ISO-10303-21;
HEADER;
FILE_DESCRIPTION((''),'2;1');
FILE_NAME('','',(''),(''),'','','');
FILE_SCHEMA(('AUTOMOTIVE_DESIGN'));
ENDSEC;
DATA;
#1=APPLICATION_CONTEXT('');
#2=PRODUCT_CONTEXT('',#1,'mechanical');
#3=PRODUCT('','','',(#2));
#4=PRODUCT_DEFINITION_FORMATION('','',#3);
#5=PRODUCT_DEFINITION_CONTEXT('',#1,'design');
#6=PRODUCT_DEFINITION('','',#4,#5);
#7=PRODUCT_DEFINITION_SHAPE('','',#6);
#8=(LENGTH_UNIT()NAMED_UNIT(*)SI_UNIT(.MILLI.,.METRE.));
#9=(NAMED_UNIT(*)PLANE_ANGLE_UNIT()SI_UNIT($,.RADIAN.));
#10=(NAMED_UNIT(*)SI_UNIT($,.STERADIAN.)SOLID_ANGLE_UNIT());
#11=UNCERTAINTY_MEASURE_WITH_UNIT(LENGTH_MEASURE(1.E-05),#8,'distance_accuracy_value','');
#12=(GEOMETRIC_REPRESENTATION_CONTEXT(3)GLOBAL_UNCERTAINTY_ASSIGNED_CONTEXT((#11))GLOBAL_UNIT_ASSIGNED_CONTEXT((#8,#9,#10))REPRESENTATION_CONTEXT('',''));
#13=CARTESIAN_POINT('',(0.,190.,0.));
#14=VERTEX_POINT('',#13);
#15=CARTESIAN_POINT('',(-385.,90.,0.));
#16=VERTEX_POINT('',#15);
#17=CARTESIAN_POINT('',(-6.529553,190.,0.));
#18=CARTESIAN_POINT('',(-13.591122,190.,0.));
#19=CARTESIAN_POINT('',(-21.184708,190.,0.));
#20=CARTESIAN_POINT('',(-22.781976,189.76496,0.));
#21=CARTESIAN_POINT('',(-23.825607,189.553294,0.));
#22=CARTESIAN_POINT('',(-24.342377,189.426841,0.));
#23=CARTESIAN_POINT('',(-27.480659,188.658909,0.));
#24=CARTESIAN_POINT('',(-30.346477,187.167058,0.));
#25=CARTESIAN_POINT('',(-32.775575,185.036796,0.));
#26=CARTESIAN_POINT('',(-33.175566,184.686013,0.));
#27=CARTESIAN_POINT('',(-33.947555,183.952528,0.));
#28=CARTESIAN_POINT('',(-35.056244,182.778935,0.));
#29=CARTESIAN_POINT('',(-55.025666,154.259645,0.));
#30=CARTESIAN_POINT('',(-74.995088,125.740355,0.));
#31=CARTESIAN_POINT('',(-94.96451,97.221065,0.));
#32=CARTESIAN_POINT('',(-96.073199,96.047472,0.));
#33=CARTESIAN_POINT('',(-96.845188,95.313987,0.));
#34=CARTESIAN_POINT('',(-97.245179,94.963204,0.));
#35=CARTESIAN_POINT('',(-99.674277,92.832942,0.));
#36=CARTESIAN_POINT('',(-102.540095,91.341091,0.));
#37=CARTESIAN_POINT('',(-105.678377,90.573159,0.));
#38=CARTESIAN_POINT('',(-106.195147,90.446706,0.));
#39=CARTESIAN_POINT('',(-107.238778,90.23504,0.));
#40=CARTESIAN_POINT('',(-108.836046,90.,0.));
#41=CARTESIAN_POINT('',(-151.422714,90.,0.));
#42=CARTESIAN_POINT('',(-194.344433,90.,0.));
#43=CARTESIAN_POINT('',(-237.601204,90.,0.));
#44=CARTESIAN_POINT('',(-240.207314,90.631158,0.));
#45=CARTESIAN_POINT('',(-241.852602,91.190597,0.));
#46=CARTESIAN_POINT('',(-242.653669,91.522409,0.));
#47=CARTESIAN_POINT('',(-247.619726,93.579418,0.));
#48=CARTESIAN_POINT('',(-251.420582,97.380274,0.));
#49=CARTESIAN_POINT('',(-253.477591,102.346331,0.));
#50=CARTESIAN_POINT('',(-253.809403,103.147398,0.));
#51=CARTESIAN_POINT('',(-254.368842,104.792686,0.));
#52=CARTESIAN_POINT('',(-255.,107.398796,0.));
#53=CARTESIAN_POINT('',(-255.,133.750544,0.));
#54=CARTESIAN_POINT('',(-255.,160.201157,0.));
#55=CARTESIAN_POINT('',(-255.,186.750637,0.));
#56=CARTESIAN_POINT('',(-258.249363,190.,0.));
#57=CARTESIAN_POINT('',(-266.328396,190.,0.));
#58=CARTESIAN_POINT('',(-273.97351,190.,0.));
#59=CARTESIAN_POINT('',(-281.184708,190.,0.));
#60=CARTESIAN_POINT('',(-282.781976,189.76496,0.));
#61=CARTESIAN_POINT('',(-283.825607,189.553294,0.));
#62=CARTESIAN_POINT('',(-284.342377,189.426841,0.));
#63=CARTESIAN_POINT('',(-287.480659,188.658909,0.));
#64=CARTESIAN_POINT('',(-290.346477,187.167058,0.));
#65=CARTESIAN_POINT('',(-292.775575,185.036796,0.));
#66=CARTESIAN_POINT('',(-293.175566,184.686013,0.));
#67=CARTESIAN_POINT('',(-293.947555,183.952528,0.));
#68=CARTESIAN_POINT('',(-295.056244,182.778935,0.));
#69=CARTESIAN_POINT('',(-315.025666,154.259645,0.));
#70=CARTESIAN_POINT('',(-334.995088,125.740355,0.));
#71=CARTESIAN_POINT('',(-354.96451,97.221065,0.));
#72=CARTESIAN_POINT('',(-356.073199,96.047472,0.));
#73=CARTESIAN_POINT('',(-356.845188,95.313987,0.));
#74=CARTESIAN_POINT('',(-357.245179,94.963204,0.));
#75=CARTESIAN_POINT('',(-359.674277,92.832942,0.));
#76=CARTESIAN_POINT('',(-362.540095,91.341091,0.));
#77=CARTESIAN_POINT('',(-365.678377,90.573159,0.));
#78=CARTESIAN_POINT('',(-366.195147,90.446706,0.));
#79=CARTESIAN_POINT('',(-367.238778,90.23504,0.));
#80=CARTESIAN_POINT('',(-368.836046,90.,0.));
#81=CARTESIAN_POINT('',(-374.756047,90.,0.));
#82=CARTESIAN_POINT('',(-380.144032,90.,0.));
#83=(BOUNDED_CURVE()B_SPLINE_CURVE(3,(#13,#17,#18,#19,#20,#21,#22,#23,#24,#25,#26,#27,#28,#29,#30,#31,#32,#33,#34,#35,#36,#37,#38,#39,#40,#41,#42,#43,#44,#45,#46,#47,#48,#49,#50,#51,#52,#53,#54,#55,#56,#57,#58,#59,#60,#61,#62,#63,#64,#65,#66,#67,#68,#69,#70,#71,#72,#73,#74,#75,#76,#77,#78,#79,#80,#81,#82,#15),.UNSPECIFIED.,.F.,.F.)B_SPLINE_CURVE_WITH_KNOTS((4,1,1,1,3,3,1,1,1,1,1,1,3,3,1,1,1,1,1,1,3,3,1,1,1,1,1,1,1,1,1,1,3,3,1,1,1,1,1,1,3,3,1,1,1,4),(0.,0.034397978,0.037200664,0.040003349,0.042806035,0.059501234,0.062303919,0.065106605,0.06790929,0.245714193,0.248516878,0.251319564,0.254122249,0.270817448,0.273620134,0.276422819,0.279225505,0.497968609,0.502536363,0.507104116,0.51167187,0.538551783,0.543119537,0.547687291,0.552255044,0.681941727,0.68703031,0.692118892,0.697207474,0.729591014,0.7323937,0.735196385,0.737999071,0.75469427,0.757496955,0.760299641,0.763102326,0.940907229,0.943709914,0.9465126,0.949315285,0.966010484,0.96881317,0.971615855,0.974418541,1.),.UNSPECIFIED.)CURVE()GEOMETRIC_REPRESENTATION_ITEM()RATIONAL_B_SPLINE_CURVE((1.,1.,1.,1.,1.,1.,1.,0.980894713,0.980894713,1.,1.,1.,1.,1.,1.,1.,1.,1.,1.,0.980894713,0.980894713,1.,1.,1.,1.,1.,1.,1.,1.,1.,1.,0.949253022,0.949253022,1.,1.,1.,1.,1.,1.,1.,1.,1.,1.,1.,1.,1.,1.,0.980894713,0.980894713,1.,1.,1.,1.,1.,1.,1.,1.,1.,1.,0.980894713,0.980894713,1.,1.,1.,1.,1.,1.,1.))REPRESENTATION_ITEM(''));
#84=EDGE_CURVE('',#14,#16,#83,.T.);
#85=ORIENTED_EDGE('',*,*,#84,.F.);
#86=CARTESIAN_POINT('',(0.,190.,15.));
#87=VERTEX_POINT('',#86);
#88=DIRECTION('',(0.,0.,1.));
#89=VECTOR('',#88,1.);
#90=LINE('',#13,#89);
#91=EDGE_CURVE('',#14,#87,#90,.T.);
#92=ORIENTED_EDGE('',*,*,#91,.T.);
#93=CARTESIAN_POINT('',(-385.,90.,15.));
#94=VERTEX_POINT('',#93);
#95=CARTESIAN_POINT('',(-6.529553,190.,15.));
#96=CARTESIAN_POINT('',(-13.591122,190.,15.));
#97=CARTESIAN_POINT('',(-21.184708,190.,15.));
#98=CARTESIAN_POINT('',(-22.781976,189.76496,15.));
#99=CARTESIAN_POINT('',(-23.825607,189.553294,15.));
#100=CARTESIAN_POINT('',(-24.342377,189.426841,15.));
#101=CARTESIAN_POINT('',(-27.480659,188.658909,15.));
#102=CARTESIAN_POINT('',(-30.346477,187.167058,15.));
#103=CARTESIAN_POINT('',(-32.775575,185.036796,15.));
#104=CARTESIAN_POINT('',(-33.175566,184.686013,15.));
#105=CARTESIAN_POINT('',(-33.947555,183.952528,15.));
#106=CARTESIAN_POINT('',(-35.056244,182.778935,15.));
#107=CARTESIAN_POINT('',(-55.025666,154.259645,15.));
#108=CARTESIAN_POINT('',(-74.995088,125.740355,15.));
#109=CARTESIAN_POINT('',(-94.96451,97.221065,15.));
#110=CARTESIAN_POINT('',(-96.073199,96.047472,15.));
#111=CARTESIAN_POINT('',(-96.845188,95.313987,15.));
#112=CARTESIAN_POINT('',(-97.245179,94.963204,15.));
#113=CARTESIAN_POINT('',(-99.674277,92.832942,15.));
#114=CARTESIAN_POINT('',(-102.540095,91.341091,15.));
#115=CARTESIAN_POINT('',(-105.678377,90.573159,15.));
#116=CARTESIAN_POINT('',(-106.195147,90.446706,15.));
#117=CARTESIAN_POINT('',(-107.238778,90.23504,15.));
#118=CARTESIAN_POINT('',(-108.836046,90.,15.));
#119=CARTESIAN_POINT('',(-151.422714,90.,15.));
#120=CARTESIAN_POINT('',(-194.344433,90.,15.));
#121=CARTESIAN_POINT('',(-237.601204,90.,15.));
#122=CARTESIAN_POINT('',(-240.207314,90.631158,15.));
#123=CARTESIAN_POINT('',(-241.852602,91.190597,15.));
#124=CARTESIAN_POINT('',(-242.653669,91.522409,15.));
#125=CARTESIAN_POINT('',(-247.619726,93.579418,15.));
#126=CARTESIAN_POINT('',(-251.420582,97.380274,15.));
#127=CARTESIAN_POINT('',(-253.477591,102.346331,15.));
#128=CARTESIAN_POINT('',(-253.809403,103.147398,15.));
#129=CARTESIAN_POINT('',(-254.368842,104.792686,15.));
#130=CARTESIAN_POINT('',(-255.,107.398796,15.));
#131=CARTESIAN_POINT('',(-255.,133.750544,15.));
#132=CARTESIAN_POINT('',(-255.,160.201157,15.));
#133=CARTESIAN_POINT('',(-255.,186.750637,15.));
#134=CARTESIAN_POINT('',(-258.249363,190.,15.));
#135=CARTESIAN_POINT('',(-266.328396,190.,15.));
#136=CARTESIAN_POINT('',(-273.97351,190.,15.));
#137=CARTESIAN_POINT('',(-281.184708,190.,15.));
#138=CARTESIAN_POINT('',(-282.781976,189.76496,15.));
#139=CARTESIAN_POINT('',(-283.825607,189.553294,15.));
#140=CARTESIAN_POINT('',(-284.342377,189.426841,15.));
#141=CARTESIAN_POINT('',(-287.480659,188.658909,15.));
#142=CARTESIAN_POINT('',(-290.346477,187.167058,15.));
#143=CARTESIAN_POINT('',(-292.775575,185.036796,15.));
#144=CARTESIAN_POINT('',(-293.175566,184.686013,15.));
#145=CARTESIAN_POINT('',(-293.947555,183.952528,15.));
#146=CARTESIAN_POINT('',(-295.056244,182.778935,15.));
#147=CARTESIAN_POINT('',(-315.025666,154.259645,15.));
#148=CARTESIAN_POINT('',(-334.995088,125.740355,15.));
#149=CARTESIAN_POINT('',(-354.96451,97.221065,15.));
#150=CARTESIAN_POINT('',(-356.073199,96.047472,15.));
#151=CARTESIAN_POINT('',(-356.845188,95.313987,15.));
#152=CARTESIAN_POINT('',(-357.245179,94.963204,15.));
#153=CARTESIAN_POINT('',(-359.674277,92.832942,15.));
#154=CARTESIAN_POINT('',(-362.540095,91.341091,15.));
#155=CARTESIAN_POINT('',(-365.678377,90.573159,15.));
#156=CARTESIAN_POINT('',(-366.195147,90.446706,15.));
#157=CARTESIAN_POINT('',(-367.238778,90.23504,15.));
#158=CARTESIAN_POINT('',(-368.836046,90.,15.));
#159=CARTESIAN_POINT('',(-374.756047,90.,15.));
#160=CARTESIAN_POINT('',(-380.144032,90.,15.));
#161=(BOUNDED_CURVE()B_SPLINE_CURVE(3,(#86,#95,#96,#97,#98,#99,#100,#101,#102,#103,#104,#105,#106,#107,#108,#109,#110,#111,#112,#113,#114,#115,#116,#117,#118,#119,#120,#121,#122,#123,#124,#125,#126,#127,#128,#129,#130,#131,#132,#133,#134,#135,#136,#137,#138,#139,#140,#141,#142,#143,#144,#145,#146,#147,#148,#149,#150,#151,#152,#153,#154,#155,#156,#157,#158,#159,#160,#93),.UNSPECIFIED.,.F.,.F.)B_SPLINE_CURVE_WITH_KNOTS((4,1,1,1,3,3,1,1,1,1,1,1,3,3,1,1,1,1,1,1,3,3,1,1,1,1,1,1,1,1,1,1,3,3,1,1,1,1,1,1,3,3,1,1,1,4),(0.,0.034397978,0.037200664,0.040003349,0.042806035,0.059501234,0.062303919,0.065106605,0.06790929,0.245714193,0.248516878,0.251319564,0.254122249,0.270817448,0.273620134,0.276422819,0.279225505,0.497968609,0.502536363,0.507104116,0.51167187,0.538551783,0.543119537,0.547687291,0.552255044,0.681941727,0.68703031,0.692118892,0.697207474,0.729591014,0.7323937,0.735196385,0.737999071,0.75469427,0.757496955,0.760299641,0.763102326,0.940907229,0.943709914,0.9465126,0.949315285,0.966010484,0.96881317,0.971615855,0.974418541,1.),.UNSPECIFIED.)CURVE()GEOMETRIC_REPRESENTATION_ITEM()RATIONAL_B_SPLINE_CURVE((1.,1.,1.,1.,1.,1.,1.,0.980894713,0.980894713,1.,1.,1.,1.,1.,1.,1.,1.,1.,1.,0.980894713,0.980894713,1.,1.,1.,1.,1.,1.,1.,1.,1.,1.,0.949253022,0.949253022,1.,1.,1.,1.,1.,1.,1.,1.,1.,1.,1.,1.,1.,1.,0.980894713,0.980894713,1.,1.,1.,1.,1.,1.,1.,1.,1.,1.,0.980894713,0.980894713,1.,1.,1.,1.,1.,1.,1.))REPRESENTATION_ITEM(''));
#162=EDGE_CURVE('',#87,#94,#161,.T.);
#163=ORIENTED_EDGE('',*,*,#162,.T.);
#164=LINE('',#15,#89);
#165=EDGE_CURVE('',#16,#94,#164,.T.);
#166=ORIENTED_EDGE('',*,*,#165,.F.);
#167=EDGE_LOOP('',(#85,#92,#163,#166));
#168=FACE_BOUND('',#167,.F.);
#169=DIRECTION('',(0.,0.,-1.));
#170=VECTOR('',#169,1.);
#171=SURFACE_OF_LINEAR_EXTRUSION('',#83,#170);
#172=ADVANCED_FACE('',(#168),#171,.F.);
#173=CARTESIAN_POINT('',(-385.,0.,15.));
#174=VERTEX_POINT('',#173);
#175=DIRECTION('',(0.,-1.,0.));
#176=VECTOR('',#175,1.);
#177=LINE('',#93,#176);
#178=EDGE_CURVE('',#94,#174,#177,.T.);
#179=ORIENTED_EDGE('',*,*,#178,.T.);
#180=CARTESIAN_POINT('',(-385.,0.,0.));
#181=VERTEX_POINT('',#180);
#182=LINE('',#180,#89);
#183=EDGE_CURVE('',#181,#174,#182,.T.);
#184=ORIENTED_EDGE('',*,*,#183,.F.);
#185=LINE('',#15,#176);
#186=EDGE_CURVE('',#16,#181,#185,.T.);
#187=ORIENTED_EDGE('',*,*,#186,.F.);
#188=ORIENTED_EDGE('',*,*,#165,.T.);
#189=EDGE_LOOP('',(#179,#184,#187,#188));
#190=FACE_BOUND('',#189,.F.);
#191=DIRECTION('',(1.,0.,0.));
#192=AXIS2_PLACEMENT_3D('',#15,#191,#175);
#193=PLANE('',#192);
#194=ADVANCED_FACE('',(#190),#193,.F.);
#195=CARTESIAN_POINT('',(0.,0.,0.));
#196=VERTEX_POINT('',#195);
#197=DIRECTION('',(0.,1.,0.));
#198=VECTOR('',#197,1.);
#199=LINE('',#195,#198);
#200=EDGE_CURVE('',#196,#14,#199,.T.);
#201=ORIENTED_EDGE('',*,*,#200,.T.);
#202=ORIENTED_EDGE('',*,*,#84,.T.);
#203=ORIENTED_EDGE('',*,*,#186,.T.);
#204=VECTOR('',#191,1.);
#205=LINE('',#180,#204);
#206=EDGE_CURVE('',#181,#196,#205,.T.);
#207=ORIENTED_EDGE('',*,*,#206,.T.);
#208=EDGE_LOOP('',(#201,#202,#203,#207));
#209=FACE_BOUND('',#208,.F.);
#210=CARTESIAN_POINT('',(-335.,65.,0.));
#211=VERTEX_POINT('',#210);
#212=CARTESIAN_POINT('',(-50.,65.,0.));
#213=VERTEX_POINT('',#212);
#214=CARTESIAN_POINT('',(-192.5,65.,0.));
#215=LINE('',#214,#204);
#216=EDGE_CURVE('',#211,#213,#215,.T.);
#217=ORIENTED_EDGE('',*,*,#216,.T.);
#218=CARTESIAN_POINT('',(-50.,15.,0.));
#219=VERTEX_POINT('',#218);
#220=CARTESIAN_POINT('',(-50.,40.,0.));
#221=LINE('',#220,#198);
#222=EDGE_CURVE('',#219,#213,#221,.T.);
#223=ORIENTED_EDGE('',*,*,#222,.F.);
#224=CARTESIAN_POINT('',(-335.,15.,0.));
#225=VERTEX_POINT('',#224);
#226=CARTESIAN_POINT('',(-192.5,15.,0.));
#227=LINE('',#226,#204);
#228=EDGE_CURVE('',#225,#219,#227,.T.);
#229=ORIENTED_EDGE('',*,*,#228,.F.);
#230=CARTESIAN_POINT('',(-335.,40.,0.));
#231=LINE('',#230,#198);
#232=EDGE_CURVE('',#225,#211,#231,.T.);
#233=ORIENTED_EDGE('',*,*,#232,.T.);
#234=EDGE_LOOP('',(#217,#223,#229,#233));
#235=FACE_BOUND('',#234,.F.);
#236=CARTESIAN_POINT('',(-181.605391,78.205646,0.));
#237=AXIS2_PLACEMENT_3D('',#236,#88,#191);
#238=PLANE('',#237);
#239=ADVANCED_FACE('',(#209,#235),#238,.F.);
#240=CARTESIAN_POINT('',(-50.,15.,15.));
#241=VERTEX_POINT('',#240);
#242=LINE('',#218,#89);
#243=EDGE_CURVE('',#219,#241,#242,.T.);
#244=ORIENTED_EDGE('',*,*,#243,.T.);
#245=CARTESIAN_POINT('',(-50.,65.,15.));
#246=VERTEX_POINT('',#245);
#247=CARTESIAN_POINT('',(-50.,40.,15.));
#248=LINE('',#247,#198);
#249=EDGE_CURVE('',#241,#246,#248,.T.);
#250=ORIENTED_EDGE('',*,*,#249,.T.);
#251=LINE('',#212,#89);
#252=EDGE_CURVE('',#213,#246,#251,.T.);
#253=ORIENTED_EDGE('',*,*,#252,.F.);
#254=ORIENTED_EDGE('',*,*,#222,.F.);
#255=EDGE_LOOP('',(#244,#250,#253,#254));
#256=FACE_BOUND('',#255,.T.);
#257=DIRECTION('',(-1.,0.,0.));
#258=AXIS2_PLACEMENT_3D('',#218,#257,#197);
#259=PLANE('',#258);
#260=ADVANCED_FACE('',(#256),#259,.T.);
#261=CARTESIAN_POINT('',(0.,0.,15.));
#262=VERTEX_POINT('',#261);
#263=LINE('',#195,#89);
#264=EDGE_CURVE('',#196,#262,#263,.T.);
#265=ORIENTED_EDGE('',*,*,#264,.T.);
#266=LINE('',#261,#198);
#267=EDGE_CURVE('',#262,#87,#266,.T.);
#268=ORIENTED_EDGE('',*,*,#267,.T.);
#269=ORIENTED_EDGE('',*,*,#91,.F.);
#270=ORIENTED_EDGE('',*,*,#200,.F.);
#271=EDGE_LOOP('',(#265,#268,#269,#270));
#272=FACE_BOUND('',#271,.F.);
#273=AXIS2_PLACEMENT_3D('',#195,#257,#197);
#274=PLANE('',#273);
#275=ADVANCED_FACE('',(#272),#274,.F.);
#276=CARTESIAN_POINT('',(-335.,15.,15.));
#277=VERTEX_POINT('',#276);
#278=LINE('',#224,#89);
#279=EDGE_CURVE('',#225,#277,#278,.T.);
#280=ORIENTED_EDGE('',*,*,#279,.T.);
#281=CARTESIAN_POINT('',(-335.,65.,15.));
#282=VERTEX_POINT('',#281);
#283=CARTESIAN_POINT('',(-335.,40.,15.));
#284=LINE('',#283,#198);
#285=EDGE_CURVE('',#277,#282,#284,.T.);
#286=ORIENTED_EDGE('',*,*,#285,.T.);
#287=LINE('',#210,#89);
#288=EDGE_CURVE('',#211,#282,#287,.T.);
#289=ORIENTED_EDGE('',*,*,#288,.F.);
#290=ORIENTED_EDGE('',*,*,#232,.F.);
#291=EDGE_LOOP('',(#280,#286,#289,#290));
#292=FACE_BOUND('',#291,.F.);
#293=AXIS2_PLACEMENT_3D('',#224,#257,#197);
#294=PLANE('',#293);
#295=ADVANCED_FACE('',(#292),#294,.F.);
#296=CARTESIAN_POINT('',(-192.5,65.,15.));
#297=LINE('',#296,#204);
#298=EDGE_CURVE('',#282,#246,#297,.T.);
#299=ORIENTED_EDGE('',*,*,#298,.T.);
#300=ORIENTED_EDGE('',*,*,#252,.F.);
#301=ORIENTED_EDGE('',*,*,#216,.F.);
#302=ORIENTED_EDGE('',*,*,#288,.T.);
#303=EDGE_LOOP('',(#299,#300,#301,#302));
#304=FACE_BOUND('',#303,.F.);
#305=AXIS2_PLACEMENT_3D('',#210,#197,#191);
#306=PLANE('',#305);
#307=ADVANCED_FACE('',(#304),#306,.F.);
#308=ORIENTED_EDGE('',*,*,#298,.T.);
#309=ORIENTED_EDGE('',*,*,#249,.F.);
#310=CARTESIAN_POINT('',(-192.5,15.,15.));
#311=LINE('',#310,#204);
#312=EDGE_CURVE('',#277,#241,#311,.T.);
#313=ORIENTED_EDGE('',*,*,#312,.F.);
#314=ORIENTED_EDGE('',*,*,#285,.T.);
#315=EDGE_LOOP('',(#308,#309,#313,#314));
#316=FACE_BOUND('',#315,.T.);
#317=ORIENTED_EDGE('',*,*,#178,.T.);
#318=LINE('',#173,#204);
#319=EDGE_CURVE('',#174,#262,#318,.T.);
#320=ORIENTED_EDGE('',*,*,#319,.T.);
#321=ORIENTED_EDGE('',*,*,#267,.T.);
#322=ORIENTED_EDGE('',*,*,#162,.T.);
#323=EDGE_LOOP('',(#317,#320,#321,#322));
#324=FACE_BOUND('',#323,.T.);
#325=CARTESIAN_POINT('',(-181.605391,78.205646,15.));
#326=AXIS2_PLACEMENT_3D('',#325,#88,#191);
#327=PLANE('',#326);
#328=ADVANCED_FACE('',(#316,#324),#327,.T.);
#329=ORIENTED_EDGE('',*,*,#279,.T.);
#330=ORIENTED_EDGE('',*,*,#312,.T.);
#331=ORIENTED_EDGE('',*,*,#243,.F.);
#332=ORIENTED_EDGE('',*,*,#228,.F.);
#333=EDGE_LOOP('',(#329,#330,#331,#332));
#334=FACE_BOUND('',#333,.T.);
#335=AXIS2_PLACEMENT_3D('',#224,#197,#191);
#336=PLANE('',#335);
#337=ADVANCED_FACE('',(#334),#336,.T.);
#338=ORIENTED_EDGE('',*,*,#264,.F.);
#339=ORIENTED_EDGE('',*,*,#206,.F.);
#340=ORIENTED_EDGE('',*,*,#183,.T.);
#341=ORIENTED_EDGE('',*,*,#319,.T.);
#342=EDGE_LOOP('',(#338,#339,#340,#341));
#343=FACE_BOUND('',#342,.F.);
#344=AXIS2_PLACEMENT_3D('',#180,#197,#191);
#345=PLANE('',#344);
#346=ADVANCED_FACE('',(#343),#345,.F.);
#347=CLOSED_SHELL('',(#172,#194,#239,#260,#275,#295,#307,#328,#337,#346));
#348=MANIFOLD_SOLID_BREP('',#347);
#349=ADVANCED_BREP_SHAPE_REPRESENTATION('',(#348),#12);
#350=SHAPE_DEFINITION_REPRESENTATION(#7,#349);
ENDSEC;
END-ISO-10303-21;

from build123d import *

# Parameters (mm, degrees)
SKETCH1_W           = 285
SKETCH1_H           = 50
BOSS_EXTRUDE1_DEPTH = 15


with BuildPart() as part:
    # Sketch1 → Boss-Extrude1 (new body)
    with BuildSketch(Plane.XY):
        with BuildLine():
            Line((0, 0), (0, 190))
            add(Edge.make_bspline(
                [(0, 190), (-6.529552996, 190), (-13.591122238, 190), (-21.184707726, 190), (-22.781976313, 189.764960178), (-23.825607074, 189.553294152), (-24.342376835, 189.426841396), (-27.480658699, 188.65890871), (-30.346477134, 187.16705806), (-32.775575291, 185.03679615), (-33.175566283, 184.686013464), (-33.947554953, 183.952527838), (-35.056243928, 182.778935313), (-55.025665916, 154.259645104), (-74.995087905, 125.740354896), (-94.964509893, 97.221064687), (-96.073198868, 96.047472162), (-96.845187538, 95.313986536), (-97.24517853, 94.96320385), (-99.674276687, 92.83294194), (-102.540095122, 91.34109129), (-105.678376985, 90.573158604), (-106.195146747, 90.446705848), (-107.238777508, 90.235039822), (-108.836046095, 90), (-151.422713642, 90), (-194.344433042, 90), (-237.601204294, 90), (-240.207313623, 90.631158439), (-241.852602178, 91.190596754), (-242.653668647, 91.52240935), (-247.619726274, 93.57941777), (-251.42058223, 97.380273726), (-253.47759065, 102.346331353), (-253.809403246, 103.147397822), (-254.368841561, 104.792686377), (-255, 107.398795706), (-255, 133.750543653), (-255, 160.201157252), (-255, 186.750636505), (-258.249363495, 190), (-266.328395744, 190), (-273.973510488, 190), (-281.184707726, 190), (-282.781976313, 189.764960178), (-283.825607074, 189.553294152), (-284.342376835, 189.426841396), (-287.480658699, 188.65890871), (-290.346477134, 187.16705806), (-292.775575291, 185.03679615), (-293.175566283, 184.686013464), (-293.947554953, 183.952527838), (-295.056243928, 182.778935313), (-315.025665916, 154.259645104), (-334.995087905, 125.740354896), (-354.964509893, 97.221064687), (-356.073198868, 96.047472162), (-356.845187538, 95.313986536), (-357.24517853, 94.96320385), (-359.674276687, 92.83294194), (-362.540095122, 91.34109129), (-365.678376985, 90.573158604), (-366.195146747, 90.446705848), (-367.238777508, 90.235039822), (-368.836046095, 90), (-374.756046976, 90), (-380.144031611, 90), (-385, 90)],
                knots=[0, 0, 0, 0, 0.034397978, 0.037200664, 0.040003349, 0.042806035, 0.042806035, 0.042806035, 0.059501234, 0.059501234, 0.059501234, 0.062303919, 0.065106605, 0.06790929, 0.245714193, 0.248516878, 0.251319564, 0.254122249, 0.254122249, 0.254122249, 0.270817448, 0.270817448, 0.270817448, 0.273620134, 0.276422819, 0.279225505, 0.497968609, 0.502536363, 0.507104116, 0.51167187, 0.51167187, 0.51167187, 0.538551783, 0.538551783, 0.538551783, 0.543119537, 0.547687291, 0.552255044, 0.681941727, 0.68703031, 0.692118892, 0.697207474, 0.729591014, 0.7323937, 0.735196385, 0.737999071, 0.737999071, 0.737999071, 0.75469427, 0.75469427, 0.75469427, 0.757496955, 0.760299641, 0.763102326, 0.940907229, 0.943709914, 0.9465126, 0.949315285, 0.949315285, 0.949315285, 0.966010484, 0.966010484, 0.966010484, 0.96881317, 0.971615855, 0.974418541, 1, 1, 1, 1], degree=3, weights=[1, 1, 1, 1, 1, 1, 1, 0.980894713, 0.980894713, 1, 1, 1, 1, 1, 1, 1, 1, 1, 1, 0.980894713, 0.980894713, 1, 1, 1, 1, 1, 1, 1, 1, 1, 1, 0.949253022, 0.949253022, 1, 1, 1, 1, 1, 1, 1, 1, 1, 1, 1, 1, 1, 1, 0.980894713, 0.980894713, 1, 1, 1, 1, 1, 1, 1, 1, 1, 1, 0.980894713, 0.980894713, 1, 1, 1, 1, 1, 1, 1]))
            Line((-385, 90), (-385, 0))
            Line((-385, 0), (0, 0))
        make_face()
        with Locations((-192.5, 40)):
            Rectangle(SKETCH1_W, SKETCH1_H, mode=Mode.SUBTRACT)
    extrude(amount=BOSS_EXTRUDE1_DEPTH)


solid = part.part
